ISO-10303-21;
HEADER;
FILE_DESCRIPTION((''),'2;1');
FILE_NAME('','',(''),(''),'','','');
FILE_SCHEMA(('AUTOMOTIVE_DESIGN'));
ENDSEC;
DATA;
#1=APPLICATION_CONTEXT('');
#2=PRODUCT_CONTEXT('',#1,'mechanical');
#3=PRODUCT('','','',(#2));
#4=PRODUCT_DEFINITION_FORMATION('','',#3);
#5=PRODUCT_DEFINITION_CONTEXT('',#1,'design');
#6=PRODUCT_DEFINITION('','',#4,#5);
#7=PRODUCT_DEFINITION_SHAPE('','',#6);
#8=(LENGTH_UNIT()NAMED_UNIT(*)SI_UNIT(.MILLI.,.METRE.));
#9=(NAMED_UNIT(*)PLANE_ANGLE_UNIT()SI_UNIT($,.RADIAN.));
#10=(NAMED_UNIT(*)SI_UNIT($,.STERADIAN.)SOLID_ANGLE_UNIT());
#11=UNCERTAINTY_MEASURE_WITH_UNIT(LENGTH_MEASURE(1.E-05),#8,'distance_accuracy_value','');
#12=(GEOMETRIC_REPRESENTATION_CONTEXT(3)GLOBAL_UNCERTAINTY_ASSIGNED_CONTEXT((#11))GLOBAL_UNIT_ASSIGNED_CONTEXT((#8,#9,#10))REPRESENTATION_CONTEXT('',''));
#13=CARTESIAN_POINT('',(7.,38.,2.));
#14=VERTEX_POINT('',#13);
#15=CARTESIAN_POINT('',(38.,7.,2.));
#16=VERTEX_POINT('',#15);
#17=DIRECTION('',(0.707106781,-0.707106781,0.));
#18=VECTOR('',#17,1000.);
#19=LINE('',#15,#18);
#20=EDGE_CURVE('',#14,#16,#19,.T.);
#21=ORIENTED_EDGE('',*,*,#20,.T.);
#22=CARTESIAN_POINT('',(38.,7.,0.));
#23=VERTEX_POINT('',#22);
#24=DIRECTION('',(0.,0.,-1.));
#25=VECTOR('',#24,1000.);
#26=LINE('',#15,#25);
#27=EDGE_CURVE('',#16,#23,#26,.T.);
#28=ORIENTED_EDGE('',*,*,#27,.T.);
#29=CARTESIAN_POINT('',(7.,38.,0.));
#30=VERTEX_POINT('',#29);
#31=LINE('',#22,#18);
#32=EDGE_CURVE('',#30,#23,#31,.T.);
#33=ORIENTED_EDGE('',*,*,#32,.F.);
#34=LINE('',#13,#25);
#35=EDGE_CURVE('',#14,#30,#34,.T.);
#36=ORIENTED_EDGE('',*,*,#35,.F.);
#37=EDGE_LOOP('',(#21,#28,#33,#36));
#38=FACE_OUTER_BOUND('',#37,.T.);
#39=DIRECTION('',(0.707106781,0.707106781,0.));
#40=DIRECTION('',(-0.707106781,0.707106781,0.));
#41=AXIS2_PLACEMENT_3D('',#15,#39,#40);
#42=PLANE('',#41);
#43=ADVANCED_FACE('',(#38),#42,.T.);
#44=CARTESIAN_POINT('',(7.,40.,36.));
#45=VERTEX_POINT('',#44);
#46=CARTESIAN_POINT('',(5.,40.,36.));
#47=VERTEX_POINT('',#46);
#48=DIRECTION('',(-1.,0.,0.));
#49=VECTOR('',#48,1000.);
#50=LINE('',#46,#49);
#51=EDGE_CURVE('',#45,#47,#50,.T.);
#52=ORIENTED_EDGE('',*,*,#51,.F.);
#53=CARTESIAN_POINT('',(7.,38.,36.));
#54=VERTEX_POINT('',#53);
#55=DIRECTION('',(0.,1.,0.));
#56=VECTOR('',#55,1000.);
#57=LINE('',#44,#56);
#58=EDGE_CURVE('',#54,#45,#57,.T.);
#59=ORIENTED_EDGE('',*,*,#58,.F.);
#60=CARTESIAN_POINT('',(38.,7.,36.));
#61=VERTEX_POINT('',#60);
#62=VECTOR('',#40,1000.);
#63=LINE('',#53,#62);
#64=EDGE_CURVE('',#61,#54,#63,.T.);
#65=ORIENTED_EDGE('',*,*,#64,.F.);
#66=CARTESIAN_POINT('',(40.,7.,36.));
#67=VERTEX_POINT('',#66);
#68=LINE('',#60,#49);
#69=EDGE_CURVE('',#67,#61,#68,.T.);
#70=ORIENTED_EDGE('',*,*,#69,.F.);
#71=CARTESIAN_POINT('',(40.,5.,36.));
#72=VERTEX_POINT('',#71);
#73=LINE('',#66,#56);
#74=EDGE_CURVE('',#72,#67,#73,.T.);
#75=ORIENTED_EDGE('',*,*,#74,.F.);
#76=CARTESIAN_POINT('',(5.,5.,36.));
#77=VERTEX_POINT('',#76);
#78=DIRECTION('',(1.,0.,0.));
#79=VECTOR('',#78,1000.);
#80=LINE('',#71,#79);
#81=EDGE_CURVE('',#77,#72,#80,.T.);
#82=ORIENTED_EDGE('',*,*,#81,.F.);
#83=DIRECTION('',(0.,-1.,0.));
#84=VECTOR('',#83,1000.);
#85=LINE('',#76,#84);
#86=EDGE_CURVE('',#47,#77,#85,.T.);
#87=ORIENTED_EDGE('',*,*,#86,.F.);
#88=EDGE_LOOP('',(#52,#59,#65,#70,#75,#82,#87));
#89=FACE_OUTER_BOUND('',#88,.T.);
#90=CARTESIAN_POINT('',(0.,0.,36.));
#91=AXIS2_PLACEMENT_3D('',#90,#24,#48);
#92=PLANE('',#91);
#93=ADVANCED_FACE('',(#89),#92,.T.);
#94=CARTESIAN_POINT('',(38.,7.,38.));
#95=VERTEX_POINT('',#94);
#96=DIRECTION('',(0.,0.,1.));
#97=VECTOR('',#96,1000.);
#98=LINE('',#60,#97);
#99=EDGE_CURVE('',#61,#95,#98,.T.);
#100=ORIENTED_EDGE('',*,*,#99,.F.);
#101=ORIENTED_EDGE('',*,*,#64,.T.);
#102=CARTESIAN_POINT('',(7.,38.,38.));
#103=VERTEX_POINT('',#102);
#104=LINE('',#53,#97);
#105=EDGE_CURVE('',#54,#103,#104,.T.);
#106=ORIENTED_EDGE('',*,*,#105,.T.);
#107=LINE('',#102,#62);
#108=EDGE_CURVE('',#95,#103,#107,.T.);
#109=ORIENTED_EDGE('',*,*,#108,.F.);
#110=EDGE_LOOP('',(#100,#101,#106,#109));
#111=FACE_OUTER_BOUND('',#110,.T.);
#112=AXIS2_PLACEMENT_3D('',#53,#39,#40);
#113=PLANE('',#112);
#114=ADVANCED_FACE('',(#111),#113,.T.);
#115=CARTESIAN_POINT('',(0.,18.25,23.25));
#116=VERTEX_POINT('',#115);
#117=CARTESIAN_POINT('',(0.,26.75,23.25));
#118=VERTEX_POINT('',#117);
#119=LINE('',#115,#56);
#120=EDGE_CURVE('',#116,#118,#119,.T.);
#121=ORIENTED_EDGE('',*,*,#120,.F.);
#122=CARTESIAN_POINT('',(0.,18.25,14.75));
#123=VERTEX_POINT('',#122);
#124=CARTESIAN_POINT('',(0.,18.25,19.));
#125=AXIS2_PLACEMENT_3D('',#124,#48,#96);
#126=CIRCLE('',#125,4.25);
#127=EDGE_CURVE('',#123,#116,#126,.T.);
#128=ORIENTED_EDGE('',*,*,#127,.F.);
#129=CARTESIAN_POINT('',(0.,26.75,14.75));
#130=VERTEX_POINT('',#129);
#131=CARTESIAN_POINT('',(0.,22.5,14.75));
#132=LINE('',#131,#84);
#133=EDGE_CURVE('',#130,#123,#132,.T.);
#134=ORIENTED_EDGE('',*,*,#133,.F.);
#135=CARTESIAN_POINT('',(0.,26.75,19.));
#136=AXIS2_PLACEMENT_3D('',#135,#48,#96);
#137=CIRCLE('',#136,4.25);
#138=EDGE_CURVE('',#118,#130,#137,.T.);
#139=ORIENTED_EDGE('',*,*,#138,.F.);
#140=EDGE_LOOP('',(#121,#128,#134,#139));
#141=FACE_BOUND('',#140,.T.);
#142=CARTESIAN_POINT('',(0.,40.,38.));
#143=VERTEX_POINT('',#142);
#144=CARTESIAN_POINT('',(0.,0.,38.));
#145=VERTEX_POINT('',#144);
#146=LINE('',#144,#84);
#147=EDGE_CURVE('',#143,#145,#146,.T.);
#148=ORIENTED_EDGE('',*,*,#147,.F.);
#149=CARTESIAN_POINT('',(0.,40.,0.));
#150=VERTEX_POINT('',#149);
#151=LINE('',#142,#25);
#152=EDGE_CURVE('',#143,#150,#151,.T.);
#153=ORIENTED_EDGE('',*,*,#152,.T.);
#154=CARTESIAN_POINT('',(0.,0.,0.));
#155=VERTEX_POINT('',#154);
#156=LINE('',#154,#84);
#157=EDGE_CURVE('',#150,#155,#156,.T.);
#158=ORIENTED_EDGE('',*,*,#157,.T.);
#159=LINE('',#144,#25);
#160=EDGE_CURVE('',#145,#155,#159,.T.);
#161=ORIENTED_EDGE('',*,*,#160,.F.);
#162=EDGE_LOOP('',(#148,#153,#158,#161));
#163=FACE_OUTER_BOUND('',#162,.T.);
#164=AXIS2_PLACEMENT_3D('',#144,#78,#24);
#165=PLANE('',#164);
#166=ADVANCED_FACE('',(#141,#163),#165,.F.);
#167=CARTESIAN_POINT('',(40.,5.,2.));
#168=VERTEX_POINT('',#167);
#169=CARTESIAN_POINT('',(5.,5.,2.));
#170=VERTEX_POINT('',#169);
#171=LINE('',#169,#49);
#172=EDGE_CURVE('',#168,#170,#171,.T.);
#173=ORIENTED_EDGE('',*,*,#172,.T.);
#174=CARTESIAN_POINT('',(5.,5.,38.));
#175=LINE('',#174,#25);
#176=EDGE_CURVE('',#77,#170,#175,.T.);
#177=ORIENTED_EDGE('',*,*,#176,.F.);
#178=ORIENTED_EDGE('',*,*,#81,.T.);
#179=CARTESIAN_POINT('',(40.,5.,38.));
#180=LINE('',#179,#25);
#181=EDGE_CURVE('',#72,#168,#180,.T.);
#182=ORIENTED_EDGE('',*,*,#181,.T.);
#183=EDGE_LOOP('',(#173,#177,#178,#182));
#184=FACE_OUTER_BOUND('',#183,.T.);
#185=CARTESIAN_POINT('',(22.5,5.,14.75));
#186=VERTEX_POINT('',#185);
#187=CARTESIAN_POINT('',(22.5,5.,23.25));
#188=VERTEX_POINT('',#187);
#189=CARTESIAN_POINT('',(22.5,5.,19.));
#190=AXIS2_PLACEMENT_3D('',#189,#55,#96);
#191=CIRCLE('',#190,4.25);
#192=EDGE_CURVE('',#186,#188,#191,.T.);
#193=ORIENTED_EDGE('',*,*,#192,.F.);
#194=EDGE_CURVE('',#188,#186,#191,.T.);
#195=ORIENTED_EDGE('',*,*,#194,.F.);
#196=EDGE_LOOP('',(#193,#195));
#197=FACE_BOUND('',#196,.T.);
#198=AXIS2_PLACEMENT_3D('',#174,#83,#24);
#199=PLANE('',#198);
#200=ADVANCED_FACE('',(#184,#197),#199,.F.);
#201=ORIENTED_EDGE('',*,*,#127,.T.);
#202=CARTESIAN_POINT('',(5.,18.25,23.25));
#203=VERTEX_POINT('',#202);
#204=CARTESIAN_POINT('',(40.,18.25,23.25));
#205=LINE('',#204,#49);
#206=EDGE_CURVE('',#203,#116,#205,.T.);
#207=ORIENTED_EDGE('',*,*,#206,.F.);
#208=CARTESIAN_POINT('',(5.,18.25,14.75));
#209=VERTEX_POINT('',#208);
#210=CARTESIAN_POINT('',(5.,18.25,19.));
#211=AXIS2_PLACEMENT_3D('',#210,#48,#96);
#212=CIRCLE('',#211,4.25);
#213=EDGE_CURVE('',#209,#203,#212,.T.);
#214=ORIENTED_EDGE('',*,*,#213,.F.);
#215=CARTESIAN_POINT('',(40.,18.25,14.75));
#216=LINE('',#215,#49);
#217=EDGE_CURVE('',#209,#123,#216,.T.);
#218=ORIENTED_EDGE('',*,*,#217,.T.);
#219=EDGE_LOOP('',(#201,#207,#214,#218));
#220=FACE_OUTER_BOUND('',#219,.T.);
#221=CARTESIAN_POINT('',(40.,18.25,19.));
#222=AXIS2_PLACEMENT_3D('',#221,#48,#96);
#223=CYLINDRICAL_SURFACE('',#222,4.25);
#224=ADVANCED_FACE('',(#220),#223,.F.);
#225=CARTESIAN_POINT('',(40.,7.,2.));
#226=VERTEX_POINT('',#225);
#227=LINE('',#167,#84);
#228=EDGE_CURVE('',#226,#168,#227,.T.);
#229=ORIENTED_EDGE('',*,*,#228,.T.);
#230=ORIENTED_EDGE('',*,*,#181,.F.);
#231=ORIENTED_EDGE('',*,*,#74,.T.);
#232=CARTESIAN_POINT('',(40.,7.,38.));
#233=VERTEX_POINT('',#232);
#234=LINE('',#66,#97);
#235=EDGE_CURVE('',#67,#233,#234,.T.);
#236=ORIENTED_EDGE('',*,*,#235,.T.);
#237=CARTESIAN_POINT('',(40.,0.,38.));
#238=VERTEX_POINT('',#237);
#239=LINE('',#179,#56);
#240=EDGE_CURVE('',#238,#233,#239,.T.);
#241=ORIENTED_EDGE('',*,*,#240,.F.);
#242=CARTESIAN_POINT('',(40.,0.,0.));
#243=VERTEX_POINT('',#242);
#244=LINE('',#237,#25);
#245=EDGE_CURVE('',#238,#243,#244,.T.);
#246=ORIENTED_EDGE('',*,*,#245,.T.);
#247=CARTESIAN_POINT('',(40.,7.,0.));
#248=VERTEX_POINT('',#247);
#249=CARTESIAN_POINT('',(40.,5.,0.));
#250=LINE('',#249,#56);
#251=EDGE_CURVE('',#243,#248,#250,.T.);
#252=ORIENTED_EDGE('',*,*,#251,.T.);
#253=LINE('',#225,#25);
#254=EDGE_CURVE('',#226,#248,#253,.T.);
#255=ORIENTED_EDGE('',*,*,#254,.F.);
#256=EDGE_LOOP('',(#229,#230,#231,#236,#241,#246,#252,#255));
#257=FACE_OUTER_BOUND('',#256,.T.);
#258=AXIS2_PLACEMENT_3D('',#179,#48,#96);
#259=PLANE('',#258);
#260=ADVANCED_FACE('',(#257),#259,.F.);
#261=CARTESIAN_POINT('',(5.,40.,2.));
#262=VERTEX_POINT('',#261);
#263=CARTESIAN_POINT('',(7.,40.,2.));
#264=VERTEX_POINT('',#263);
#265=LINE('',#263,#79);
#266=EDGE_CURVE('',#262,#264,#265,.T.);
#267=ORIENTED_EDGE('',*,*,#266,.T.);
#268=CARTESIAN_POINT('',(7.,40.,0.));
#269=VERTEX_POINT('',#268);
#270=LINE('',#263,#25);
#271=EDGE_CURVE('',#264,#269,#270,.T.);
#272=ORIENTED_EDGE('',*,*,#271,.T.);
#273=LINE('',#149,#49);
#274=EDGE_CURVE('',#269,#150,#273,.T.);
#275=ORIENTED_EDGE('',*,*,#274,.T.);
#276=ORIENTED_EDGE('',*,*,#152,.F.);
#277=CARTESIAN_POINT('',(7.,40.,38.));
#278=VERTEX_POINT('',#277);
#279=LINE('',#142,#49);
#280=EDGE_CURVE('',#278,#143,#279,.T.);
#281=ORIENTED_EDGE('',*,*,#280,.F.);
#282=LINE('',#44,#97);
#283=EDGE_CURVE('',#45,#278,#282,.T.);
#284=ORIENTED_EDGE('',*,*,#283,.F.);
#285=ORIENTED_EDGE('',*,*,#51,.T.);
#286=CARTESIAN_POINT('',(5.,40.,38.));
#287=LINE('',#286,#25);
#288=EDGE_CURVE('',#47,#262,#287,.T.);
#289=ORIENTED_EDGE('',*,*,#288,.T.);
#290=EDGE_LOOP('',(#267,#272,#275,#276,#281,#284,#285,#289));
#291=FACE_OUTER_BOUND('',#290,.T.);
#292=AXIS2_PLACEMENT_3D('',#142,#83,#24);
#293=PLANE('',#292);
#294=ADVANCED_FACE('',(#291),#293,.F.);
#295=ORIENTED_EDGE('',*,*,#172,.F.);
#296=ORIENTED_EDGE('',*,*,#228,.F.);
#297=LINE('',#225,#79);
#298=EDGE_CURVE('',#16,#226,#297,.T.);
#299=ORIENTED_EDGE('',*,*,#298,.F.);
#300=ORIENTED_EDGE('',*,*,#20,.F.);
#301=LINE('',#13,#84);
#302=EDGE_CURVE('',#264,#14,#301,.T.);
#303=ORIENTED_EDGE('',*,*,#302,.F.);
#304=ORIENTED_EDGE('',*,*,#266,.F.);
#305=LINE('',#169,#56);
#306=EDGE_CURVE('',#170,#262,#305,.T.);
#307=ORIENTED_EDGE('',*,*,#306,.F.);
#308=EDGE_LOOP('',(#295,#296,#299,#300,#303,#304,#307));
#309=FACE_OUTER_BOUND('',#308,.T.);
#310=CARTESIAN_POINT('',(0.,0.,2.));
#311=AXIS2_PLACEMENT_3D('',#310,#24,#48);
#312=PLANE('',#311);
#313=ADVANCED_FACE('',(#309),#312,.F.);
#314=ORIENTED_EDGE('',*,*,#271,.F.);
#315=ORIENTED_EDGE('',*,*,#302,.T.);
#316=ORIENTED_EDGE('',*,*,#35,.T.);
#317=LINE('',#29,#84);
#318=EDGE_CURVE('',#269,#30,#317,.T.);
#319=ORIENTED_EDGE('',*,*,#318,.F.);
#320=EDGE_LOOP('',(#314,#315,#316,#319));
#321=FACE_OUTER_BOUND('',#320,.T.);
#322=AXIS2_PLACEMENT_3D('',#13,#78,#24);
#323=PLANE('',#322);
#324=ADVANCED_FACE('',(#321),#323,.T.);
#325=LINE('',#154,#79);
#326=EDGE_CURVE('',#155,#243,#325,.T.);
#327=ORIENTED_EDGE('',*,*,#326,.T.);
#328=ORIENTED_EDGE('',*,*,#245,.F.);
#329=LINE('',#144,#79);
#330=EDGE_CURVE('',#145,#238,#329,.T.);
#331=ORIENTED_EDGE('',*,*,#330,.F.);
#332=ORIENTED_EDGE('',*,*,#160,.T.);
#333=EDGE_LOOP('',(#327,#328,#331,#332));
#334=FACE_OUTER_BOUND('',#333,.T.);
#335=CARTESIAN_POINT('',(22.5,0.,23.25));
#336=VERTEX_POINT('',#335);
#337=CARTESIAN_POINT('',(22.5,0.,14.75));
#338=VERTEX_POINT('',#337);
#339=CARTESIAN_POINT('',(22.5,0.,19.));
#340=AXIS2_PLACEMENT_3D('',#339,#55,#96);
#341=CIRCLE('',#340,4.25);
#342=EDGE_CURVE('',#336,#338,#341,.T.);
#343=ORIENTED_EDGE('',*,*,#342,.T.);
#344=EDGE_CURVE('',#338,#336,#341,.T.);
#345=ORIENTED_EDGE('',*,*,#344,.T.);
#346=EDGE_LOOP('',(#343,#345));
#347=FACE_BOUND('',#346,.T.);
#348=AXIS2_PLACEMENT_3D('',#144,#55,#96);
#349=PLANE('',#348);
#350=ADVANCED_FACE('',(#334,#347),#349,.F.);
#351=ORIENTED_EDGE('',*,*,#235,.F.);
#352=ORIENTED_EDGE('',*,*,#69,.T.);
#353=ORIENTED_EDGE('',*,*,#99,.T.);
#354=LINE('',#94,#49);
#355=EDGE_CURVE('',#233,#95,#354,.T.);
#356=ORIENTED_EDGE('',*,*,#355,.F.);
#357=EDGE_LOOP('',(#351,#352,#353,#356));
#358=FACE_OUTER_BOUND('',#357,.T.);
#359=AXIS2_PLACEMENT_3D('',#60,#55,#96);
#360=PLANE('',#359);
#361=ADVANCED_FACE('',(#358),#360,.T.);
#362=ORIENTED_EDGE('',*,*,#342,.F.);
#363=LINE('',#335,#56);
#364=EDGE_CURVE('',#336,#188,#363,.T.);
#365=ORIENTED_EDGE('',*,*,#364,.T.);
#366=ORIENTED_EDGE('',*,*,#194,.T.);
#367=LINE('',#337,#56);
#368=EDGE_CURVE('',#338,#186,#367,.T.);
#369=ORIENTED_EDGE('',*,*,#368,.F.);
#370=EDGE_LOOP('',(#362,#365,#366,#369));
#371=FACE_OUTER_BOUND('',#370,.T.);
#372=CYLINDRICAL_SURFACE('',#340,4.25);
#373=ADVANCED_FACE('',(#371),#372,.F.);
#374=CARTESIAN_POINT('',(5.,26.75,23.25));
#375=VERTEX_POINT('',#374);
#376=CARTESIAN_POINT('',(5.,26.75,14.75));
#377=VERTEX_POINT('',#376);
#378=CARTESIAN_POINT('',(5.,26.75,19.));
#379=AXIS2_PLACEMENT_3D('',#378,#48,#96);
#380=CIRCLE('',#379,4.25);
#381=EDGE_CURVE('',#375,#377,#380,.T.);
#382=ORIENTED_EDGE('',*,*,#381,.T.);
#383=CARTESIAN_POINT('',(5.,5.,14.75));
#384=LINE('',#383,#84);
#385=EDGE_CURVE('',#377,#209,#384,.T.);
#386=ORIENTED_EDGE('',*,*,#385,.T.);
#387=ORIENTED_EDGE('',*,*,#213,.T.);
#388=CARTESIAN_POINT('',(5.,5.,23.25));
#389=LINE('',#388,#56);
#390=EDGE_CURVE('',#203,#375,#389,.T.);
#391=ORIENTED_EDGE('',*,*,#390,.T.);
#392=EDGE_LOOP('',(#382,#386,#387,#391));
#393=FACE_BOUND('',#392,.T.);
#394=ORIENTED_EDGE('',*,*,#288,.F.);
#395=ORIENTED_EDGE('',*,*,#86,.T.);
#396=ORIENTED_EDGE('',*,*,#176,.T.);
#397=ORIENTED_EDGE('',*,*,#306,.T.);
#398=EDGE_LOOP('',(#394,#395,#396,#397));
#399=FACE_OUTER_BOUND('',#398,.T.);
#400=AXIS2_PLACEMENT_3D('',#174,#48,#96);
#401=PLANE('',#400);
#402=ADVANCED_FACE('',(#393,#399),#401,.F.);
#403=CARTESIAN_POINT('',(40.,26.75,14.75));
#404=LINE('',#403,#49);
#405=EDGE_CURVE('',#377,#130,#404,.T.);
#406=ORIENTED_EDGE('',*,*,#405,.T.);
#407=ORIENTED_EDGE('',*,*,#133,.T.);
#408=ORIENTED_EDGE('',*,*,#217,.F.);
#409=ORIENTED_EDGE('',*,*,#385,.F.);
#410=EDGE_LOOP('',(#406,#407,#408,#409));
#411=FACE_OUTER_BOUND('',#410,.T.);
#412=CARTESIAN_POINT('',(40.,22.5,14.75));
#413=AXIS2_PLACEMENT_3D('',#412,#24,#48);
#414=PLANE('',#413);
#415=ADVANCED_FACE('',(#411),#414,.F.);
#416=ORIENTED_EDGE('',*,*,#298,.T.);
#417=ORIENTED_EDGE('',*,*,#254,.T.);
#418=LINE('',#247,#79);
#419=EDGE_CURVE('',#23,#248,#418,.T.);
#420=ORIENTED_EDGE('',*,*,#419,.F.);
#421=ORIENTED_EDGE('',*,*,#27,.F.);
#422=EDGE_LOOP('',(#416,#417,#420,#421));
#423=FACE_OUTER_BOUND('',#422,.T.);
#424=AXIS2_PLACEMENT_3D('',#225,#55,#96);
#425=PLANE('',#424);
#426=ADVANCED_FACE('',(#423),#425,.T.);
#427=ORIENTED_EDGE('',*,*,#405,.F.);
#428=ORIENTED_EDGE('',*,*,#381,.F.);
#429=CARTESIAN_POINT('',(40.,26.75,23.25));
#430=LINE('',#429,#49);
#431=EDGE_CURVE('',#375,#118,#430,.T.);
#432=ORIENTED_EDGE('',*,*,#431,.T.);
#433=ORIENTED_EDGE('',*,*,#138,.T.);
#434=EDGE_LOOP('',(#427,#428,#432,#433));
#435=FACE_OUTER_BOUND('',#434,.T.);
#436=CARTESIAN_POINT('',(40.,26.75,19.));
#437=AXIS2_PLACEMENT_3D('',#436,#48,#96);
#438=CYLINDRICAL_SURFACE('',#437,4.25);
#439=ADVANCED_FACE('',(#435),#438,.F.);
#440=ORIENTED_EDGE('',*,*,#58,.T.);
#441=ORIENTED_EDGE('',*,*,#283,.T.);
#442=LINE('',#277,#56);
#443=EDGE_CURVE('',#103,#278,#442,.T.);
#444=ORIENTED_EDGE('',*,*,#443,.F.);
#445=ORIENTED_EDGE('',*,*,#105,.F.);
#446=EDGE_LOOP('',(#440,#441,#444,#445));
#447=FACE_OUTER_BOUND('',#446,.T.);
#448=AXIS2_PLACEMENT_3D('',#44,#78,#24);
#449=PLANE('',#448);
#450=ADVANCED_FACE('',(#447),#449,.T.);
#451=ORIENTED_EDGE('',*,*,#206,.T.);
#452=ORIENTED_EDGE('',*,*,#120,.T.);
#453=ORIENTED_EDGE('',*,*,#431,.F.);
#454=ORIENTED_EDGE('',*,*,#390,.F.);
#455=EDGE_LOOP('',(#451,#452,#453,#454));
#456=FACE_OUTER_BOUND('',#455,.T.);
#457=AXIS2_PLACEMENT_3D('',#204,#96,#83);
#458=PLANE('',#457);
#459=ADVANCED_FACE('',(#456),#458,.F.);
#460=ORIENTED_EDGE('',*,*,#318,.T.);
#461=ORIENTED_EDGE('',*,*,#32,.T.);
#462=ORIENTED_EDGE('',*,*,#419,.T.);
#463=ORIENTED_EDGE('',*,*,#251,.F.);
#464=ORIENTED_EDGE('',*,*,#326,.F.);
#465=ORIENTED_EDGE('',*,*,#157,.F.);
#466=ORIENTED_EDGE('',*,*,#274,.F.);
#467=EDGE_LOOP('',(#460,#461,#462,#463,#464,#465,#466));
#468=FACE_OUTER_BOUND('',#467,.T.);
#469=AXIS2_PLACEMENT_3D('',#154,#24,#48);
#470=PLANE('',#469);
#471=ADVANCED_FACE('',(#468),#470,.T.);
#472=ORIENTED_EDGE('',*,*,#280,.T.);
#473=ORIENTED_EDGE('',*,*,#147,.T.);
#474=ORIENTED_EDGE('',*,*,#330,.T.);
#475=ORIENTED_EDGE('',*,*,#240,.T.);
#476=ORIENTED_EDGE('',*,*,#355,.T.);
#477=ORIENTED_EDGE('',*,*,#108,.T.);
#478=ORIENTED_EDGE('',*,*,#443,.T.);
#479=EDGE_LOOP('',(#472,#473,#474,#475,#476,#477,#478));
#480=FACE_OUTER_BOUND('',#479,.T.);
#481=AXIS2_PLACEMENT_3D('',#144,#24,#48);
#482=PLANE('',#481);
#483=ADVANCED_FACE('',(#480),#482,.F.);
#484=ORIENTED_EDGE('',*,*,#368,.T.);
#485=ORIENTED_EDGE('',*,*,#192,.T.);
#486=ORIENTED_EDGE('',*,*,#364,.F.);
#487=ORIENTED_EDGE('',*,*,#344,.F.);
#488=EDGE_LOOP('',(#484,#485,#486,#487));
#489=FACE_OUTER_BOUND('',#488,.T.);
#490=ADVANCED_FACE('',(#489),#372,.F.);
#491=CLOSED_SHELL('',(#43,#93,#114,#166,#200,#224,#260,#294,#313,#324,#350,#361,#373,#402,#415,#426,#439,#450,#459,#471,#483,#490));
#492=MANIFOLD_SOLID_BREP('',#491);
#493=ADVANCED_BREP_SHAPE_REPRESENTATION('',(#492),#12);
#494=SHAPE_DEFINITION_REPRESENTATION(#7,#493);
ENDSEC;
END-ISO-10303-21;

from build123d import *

# Parameters (mm, degrees)
BOSS_EXTRUDE1_DEPTH = 38
BOSS_EXTRUDE2_DEPTH = 2
BOSS_EXTRUDE3_DEPTH = 2
SKETCH4_R           = 4.25
CUT_EXTRUDE1_DEPTH  = 66.337584896
CUT_EXTRUDE2_DEPTH  = 69.14690015


with BuildPart() as part:
    # Sketch1 → Boss-Extrude1 (new body)
    with BuildSketch(Plane.XY):
        Polygon((0, 0), (40, 0), (40, 5), (5, 5), (5, 40), (0, 40), align=None)
    extrude(amount=BOSS_EXTRUDE1_DEPTH)

    # Sketch2 → Boss-Extrude2 (add)
    with BuildSketch(Plane.XY.offset(38)):
        Polygon((7, 40), (7, 38), (38, 7), (40, 7), (40, 5), (5, 5), (5, 40), align=None)
    extrude(amount=-BOSS_EXTRUDE2_DEPTH)

    # Sketch3 → Boss-Extrude3 (add)
    with BuildSketch(Plane(origin=(0, 0, 0), x_dir=(-1, 0, 0), z_dir=(0, 0, -1))):
        Polygon((-38, 7), (-7, 38), (-7, 40), (-5, 40), (-5, 5), (-40, 5), (-40, 7), align=None)
    extrude(amount=-BOSS_EXTRUDE3_DEPTH)

    # Sketch4 → Cut-Extrude1 (cut, through all)
    with BuildSketch(Plane(origin=(0, 5, 0), x_dir=(1, 0, 0), z_dir=(0, 1, 0))):
        with Locations(Location((22.5, -19, 0), (0, 0, 270))):
            Circle(SKETCH4_R)
    extrude(amount=-CUT_EXTRUDE1_DEPTH, mode=Mode.SUBTRACT)

    # Sketch5 → Cut-Extrude2 (cut, through all)
    with BuildSketch(Plane.ZY):
        with BuildLine():
            Line((14.75, 22.5), (14.75, 18.25))
            ThreePointArc((14.75, 18.25), (19, 14), (23.25, 18.25))
            Line((23.25, 18.25), (23.25, 26.75))
            ThreePointArc((23.25, 26.75), (19, 31), (14.75, 26.75))
            Line((14.75, 26.75), (14.75, 22.5))
        make_face()
    extrude(amount=-CUT_EXTRUDE2_DEPTH, mode=Mode.SUBTRACT)


solid = part.part
